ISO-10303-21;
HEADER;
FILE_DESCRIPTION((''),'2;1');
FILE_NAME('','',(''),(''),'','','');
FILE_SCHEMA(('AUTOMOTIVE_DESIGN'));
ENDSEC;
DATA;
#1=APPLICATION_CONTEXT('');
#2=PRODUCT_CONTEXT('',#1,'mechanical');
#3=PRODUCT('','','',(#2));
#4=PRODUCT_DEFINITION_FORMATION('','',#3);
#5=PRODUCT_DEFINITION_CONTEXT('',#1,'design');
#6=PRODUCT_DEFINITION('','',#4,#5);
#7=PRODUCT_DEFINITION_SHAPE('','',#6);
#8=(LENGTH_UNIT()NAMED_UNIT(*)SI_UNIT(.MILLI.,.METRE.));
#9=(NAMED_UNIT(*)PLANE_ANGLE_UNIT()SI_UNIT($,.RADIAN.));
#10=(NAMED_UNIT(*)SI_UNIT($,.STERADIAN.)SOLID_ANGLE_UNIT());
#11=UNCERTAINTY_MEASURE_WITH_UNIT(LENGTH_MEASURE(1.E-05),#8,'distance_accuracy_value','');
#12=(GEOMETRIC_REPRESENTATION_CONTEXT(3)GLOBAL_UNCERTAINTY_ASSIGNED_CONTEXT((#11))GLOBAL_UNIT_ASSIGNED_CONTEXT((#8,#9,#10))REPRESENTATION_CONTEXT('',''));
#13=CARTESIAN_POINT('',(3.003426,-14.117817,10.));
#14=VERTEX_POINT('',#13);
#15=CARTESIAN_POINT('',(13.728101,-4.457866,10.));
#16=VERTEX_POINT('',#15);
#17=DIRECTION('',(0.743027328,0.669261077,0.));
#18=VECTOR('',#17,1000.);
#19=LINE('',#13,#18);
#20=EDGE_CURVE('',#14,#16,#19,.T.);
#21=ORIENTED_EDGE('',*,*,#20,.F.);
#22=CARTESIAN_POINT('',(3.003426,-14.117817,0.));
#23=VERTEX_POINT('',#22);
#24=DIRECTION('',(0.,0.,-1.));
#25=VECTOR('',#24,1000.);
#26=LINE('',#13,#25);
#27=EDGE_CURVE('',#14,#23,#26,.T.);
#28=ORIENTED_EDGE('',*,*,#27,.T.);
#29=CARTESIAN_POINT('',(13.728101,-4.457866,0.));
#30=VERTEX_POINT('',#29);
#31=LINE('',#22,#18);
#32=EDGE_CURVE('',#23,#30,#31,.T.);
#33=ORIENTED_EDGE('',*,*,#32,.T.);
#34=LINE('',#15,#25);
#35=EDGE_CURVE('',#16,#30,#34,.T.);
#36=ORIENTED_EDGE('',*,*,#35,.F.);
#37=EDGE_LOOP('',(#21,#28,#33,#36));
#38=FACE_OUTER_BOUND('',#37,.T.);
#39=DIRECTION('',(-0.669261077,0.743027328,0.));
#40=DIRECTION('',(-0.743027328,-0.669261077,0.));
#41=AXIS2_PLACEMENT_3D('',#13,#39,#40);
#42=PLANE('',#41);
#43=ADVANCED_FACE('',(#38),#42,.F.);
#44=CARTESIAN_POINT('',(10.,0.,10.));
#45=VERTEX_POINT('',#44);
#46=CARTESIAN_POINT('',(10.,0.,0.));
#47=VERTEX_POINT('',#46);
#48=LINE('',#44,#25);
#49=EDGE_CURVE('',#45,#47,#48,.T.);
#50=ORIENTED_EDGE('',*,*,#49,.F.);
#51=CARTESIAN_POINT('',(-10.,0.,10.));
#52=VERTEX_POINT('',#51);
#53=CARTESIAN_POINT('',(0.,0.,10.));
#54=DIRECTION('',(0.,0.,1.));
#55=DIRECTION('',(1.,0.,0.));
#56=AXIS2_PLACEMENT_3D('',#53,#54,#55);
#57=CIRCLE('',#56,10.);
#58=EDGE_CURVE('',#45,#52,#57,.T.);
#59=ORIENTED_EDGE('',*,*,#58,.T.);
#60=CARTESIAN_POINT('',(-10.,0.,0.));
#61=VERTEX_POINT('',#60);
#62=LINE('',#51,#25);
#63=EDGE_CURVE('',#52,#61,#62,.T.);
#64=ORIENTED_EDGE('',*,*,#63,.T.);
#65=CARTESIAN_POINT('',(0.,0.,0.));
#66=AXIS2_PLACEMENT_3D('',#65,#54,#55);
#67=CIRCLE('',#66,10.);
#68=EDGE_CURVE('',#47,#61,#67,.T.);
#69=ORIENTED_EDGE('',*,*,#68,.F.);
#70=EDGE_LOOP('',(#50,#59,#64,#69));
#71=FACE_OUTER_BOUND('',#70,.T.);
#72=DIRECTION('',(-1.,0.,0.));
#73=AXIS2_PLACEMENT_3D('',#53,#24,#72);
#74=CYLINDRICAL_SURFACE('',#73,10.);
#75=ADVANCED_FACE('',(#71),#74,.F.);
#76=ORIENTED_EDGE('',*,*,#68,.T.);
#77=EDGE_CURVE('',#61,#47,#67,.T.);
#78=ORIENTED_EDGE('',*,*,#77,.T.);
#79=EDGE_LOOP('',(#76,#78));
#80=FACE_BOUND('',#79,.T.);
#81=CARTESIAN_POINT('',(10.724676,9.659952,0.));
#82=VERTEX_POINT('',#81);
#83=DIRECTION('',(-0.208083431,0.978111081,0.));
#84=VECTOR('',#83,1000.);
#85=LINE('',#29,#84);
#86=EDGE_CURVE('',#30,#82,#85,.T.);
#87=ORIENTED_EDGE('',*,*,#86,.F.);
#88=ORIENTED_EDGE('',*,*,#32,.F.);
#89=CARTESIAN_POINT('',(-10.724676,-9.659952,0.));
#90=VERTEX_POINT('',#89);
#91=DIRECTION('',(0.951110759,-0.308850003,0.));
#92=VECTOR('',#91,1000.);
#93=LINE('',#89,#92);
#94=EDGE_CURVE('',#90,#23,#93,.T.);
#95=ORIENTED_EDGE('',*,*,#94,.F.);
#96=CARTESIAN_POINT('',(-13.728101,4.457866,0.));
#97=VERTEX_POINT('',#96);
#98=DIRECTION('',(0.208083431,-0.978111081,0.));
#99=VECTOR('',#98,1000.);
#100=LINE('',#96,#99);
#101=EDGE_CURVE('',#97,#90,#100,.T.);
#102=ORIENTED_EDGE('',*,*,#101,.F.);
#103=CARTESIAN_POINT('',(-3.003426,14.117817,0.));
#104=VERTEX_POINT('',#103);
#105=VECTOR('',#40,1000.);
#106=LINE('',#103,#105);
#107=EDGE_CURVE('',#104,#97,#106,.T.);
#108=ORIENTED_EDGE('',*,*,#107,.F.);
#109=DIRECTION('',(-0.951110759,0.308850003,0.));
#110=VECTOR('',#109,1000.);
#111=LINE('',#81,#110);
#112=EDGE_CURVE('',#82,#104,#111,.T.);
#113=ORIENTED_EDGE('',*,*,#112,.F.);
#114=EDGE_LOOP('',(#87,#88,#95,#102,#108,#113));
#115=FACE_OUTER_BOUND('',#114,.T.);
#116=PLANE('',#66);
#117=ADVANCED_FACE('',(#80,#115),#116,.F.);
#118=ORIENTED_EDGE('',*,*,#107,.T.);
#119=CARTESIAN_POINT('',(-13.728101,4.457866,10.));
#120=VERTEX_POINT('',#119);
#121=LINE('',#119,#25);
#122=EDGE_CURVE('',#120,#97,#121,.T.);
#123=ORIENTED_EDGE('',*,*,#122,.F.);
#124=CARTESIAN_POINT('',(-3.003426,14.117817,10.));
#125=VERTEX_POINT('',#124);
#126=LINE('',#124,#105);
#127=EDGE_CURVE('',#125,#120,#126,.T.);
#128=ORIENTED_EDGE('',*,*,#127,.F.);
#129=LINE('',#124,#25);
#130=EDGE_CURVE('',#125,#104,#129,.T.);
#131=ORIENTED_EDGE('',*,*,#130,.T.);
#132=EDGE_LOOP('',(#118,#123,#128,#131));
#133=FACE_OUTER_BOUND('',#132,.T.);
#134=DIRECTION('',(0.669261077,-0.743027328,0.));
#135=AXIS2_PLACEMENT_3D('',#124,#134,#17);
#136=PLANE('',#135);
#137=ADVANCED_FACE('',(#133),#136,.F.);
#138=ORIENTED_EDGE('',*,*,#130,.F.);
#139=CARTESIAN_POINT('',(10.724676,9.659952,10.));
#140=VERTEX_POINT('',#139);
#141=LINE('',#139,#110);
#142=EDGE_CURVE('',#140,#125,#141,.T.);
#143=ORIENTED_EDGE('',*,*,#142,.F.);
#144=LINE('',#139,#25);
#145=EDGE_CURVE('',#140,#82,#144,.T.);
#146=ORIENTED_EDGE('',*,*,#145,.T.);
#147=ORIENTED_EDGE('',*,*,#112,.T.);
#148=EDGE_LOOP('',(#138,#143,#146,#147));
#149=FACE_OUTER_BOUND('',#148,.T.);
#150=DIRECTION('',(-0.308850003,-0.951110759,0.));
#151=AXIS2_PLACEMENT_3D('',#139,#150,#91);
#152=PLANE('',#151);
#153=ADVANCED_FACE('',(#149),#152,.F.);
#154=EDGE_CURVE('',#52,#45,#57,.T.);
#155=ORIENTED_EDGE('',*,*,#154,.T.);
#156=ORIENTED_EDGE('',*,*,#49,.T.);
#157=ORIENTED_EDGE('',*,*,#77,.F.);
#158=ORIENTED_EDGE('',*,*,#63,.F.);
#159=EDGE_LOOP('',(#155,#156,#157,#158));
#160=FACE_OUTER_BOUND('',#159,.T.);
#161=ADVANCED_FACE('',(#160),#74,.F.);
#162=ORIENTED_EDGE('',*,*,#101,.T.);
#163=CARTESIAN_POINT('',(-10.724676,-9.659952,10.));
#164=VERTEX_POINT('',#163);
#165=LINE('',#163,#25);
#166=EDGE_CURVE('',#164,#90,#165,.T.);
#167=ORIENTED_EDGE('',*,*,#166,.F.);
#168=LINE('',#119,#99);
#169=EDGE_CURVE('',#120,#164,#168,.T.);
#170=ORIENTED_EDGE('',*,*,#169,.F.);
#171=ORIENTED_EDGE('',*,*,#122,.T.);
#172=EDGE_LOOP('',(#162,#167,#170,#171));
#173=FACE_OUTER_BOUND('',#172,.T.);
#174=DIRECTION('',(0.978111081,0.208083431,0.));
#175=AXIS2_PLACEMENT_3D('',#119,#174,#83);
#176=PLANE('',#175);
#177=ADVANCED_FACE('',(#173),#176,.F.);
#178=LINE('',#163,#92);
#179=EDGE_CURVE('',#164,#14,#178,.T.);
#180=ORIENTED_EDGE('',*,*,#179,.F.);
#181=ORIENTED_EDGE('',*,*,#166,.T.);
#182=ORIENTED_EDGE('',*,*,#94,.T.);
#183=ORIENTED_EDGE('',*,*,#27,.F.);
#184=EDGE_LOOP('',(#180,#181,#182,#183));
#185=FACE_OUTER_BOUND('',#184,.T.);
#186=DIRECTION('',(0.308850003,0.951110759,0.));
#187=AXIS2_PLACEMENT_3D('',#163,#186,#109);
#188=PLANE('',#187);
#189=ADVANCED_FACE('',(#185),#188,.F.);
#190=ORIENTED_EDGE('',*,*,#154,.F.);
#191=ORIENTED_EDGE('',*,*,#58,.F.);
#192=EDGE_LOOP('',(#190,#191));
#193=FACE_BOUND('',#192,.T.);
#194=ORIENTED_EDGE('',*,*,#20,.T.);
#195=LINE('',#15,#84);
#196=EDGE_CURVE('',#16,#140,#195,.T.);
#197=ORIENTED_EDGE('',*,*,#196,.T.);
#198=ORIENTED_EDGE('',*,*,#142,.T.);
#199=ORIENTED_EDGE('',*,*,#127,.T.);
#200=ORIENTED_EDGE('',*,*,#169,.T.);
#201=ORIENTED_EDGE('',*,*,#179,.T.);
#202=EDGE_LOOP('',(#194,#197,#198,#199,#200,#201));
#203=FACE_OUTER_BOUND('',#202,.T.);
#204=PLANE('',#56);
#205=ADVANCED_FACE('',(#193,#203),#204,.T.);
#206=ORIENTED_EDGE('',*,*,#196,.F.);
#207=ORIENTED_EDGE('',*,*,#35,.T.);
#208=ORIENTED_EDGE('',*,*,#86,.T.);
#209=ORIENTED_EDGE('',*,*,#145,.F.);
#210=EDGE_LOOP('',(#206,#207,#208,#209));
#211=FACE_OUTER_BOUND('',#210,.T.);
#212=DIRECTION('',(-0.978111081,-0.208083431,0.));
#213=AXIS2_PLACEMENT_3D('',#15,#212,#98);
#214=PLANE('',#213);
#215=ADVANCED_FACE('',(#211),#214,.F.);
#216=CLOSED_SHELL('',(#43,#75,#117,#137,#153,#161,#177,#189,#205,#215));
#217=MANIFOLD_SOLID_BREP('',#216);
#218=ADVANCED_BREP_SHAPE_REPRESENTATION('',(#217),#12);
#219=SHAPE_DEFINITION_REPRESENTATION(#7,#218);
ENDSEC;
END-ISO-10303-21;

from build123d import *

# Parameters (mm, degrees)
SKETCH1_R           = 10
BOSS_EXTRUDE1_DEPTH = 10


with BuildPart() as part:
    # Sketch1 → Boss-Extrude1 (new body)
    with BuildSketch(Plane.XY):
        Polygon((10.724675699, 9.659951577), (-3.003425616, 14.117817392), (-13.728101315, 4.457865814), (-10.724675699, -9.659951577), (3.003425616, -14.117817392), (13.728101315, -4.457865814), align=None)
        Circle(SKETCH1_R, mode=Mode.SUBTRACT)
    extrude(amount=BOSS_EXTRUDE1_DEPTH)


solid = part.part
